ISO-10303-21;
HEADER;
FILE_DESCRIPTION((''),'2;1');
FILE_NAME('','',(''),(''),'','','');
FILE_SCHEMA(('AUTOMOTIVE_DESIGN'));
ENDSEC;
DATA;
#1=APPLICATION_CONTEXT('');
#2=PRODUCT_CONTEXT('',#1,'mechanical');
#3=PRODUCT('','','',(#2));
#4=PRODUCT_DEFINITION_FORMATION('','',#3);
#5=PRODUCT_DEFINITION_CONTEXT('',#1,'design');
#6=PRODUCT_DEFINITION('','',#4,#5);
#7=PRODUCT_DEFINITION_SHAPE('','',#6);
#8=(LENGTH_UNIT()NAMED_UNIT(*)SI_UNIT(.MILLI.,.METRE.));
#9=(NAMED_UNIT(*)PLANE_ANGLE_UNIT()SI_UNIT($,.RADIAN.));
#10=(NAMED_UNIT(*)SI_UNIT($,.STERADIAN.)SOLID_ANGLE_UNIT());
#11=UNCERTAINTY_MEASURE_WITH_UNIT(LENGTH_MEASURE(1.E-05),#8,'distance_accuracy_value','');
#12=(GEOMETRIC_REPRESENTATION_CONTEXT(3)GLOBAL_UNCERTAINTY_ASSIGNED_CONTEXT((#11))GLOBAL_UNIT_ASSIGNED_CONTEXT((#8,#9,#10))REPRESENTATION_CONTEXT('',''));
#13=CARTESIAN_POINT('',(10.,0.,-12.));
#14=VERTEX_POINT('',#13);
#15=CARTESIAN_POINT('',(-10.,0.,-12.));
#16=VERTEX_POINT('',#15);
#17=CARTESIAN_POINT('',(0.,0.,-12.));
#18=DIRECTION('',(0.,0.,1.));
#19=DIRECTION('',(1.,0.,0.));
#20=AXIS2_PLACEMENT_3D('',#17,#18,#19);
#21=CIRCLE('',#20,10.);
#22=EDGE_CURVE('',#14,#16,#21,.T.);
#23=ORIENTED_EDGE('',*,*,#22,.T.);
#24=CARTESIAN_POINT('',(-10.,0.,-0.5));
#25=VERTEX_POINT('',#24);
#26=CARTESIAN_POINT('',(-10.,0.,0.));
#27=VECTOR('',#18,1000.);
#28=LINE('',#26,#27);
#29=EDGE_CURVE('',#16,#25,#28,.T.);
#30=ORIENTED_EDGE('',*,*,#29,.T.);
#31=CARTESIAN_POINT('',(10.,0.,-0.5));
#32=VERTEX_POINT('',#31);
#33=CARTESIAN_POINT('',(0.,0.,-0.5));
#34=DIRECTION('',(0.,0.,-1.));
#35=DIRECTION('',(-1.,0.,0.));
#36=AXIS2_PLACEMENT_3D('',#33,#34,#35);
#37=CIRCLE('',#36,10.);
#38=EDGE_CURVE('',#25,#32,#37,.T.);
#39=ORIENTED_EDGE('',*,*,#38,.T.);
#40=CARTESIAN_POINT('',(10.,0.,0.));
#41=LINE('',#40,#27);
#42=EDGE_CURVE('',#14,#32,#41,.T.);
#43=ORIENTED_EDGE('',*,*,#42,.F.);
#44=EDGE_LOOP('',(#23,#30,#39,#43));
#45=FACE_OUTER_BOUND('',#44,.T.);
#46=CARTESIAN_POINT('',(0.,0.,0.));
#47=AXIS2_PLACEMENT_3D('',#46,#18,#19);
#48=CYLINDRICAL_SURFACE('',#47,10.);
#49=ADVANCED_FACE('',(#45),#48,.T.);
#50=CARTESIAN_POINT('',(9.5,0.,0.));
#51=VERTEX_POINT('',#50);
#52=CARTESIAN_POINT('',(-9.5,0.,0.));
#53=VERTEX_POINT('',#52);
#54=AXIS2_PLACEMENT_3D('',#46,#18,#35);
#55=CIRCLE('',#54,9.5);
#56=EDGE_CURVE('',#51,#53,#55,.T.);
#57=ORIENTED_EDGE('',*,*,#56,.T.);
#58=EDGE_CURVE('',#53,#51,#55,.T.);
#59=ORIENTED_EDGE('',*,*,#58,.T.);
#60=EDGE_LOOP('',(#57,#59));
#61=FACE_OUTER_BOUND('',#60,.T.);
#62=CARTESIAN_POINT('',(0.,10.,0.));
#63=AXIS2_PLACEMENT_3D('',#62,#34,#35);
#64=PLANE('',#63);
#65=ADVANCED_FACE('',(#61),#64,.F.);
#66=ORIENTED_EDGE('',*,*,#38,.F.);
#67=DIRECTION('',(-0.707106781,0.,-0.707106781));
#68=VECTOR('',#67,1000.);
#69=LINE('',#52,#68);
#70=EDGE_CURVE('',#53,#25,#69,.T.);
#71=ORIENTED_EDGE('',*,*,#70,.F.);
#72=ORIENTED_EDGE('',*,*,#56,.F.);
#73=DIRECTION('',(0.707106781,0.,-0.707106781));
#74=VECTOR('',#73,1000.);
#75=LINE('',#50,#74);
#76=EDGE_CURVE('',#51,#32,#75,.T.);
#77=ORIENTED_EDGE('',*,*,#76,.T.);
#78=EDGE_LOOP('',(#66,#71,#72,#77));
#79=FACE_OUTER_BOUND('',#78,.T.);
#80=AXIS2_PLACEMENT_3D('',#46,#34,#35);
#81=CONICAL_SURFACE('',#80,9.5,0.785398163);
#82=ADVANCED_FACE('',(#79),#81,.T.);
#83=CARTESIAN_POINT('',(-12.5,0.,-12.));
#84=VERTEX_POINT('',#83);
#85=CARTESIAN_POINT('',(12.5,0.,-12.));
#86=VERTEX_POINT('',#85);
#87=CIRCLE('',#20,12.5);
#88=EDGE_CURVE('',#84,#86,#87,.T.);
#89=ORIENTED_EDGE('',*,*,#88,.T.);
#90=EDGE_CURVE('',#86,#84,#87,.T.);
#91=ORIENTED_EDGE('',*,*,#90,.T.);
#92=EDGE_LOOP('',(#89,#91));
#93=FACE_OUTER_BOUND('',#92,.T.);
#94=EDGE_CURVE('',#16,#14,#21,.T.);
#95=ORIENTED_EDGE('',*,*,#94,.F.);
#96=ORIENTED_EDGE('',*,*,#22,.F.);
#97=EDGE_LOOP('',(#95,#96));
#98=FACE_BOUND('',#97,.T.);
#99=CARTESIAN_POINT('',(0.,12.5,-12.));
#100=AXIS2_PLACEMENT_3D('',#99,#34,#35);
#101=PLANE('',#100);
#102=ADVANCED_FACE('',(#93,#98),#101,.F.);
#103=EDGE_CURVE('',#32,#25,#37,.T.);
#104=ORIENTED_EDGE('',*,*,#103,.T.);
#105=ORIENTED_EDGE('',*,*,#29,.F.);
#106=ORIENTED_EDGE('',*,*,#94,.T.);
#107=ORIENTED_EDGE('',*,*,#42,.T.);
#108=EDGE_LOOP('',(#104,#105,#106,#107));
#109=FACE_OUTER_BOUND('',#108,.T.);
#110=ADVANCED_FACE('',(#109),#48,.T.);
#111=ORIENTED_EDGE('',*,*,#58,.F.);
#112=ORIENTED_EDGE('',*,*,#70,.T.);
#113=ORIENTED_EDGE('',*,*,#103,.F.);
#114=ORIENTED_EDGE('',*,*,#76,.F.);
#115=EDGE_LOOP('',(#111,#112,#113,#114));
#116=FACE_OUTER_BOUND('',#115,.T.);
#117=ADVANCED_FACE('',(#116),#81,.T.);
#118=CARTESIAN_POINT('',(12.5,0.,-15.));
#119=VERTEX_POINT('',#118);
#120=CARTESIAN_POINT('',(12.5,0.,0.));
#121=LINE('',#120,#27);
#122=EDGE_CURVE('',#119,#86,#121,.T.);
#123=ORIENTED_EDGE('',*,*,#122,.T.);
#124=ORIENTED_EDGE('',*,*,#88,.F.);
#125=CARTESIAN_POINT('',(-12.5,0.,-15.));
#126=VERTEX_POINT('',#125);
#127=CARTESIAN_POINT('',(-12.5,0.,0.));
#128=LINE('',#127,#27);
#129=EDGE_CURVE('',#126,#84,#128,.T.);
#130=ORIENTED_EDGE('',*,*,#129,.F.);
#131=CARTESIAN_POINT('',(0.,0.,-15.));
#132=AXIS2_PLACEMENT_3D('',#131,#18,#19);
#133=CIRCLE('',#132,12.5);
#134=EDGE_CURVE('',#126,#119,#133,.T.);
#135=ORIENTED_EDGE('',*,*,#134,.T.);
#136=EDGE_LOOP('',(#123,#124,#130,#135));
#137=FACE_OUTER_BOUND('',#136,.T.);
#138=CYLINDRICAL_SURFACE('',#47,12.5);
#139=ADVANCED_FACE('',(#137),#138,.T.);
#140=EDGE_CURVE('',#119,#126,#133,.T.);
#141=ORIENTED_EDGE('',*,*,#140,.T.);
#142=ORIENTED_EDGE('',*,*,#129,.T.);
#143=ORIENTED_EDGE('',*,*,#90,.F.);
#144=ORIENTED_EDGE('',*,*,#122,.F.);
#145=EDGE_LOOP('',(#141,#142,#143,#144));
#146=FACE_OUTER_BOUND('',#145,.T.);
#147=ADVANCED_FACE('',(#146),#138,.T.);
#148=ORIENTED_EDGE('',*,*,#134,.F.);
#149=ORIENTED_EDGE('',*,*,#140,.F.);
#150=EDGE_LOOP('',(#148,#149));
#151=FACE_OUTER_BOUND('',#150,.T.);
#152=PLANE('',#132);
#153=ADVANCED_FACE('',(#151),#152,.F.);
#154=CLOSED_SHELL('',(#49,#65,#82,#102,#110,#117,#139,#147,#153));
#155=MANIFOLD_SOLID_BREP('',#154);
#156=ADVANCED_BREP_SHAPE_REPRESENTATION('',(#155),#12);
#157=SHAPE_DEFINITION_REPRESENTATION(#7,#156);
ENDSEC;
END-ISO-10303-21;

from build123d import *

# Parameters (mm, degrees)
CHAMFER1_SIZE = 0.5


with BuildPart() as part:
    # Sketch1 → Revolve1 (revolve)
    with BuildSketch(Plane(origin=(0, 0, 0), x_dir=(0, 0, -1), z_dir=(1, 0, 0)), mode=Mode.PRIVATE) as revolve1_sk:
        Polygon((15, 0), (15, 12.5), (12, 12.5), (12, 10), (0, 10), (0, 0), align=None)
    revolve(revolve1_sk.sketch.rotate(Axis((0, 0, 0), (0, 0, -1)), 90), axis=Axis((0, 0, 0), (0, 0, -1)))

    # Chamfer1
    chamfer1_edges = [part.edges().sort_by_distance(p)[0] for p in [
        (-10, 0, 0),
    ]]
    chamfer(chamfer1_edges, length=CHAMFER1_SIZE)


solid = part.part
